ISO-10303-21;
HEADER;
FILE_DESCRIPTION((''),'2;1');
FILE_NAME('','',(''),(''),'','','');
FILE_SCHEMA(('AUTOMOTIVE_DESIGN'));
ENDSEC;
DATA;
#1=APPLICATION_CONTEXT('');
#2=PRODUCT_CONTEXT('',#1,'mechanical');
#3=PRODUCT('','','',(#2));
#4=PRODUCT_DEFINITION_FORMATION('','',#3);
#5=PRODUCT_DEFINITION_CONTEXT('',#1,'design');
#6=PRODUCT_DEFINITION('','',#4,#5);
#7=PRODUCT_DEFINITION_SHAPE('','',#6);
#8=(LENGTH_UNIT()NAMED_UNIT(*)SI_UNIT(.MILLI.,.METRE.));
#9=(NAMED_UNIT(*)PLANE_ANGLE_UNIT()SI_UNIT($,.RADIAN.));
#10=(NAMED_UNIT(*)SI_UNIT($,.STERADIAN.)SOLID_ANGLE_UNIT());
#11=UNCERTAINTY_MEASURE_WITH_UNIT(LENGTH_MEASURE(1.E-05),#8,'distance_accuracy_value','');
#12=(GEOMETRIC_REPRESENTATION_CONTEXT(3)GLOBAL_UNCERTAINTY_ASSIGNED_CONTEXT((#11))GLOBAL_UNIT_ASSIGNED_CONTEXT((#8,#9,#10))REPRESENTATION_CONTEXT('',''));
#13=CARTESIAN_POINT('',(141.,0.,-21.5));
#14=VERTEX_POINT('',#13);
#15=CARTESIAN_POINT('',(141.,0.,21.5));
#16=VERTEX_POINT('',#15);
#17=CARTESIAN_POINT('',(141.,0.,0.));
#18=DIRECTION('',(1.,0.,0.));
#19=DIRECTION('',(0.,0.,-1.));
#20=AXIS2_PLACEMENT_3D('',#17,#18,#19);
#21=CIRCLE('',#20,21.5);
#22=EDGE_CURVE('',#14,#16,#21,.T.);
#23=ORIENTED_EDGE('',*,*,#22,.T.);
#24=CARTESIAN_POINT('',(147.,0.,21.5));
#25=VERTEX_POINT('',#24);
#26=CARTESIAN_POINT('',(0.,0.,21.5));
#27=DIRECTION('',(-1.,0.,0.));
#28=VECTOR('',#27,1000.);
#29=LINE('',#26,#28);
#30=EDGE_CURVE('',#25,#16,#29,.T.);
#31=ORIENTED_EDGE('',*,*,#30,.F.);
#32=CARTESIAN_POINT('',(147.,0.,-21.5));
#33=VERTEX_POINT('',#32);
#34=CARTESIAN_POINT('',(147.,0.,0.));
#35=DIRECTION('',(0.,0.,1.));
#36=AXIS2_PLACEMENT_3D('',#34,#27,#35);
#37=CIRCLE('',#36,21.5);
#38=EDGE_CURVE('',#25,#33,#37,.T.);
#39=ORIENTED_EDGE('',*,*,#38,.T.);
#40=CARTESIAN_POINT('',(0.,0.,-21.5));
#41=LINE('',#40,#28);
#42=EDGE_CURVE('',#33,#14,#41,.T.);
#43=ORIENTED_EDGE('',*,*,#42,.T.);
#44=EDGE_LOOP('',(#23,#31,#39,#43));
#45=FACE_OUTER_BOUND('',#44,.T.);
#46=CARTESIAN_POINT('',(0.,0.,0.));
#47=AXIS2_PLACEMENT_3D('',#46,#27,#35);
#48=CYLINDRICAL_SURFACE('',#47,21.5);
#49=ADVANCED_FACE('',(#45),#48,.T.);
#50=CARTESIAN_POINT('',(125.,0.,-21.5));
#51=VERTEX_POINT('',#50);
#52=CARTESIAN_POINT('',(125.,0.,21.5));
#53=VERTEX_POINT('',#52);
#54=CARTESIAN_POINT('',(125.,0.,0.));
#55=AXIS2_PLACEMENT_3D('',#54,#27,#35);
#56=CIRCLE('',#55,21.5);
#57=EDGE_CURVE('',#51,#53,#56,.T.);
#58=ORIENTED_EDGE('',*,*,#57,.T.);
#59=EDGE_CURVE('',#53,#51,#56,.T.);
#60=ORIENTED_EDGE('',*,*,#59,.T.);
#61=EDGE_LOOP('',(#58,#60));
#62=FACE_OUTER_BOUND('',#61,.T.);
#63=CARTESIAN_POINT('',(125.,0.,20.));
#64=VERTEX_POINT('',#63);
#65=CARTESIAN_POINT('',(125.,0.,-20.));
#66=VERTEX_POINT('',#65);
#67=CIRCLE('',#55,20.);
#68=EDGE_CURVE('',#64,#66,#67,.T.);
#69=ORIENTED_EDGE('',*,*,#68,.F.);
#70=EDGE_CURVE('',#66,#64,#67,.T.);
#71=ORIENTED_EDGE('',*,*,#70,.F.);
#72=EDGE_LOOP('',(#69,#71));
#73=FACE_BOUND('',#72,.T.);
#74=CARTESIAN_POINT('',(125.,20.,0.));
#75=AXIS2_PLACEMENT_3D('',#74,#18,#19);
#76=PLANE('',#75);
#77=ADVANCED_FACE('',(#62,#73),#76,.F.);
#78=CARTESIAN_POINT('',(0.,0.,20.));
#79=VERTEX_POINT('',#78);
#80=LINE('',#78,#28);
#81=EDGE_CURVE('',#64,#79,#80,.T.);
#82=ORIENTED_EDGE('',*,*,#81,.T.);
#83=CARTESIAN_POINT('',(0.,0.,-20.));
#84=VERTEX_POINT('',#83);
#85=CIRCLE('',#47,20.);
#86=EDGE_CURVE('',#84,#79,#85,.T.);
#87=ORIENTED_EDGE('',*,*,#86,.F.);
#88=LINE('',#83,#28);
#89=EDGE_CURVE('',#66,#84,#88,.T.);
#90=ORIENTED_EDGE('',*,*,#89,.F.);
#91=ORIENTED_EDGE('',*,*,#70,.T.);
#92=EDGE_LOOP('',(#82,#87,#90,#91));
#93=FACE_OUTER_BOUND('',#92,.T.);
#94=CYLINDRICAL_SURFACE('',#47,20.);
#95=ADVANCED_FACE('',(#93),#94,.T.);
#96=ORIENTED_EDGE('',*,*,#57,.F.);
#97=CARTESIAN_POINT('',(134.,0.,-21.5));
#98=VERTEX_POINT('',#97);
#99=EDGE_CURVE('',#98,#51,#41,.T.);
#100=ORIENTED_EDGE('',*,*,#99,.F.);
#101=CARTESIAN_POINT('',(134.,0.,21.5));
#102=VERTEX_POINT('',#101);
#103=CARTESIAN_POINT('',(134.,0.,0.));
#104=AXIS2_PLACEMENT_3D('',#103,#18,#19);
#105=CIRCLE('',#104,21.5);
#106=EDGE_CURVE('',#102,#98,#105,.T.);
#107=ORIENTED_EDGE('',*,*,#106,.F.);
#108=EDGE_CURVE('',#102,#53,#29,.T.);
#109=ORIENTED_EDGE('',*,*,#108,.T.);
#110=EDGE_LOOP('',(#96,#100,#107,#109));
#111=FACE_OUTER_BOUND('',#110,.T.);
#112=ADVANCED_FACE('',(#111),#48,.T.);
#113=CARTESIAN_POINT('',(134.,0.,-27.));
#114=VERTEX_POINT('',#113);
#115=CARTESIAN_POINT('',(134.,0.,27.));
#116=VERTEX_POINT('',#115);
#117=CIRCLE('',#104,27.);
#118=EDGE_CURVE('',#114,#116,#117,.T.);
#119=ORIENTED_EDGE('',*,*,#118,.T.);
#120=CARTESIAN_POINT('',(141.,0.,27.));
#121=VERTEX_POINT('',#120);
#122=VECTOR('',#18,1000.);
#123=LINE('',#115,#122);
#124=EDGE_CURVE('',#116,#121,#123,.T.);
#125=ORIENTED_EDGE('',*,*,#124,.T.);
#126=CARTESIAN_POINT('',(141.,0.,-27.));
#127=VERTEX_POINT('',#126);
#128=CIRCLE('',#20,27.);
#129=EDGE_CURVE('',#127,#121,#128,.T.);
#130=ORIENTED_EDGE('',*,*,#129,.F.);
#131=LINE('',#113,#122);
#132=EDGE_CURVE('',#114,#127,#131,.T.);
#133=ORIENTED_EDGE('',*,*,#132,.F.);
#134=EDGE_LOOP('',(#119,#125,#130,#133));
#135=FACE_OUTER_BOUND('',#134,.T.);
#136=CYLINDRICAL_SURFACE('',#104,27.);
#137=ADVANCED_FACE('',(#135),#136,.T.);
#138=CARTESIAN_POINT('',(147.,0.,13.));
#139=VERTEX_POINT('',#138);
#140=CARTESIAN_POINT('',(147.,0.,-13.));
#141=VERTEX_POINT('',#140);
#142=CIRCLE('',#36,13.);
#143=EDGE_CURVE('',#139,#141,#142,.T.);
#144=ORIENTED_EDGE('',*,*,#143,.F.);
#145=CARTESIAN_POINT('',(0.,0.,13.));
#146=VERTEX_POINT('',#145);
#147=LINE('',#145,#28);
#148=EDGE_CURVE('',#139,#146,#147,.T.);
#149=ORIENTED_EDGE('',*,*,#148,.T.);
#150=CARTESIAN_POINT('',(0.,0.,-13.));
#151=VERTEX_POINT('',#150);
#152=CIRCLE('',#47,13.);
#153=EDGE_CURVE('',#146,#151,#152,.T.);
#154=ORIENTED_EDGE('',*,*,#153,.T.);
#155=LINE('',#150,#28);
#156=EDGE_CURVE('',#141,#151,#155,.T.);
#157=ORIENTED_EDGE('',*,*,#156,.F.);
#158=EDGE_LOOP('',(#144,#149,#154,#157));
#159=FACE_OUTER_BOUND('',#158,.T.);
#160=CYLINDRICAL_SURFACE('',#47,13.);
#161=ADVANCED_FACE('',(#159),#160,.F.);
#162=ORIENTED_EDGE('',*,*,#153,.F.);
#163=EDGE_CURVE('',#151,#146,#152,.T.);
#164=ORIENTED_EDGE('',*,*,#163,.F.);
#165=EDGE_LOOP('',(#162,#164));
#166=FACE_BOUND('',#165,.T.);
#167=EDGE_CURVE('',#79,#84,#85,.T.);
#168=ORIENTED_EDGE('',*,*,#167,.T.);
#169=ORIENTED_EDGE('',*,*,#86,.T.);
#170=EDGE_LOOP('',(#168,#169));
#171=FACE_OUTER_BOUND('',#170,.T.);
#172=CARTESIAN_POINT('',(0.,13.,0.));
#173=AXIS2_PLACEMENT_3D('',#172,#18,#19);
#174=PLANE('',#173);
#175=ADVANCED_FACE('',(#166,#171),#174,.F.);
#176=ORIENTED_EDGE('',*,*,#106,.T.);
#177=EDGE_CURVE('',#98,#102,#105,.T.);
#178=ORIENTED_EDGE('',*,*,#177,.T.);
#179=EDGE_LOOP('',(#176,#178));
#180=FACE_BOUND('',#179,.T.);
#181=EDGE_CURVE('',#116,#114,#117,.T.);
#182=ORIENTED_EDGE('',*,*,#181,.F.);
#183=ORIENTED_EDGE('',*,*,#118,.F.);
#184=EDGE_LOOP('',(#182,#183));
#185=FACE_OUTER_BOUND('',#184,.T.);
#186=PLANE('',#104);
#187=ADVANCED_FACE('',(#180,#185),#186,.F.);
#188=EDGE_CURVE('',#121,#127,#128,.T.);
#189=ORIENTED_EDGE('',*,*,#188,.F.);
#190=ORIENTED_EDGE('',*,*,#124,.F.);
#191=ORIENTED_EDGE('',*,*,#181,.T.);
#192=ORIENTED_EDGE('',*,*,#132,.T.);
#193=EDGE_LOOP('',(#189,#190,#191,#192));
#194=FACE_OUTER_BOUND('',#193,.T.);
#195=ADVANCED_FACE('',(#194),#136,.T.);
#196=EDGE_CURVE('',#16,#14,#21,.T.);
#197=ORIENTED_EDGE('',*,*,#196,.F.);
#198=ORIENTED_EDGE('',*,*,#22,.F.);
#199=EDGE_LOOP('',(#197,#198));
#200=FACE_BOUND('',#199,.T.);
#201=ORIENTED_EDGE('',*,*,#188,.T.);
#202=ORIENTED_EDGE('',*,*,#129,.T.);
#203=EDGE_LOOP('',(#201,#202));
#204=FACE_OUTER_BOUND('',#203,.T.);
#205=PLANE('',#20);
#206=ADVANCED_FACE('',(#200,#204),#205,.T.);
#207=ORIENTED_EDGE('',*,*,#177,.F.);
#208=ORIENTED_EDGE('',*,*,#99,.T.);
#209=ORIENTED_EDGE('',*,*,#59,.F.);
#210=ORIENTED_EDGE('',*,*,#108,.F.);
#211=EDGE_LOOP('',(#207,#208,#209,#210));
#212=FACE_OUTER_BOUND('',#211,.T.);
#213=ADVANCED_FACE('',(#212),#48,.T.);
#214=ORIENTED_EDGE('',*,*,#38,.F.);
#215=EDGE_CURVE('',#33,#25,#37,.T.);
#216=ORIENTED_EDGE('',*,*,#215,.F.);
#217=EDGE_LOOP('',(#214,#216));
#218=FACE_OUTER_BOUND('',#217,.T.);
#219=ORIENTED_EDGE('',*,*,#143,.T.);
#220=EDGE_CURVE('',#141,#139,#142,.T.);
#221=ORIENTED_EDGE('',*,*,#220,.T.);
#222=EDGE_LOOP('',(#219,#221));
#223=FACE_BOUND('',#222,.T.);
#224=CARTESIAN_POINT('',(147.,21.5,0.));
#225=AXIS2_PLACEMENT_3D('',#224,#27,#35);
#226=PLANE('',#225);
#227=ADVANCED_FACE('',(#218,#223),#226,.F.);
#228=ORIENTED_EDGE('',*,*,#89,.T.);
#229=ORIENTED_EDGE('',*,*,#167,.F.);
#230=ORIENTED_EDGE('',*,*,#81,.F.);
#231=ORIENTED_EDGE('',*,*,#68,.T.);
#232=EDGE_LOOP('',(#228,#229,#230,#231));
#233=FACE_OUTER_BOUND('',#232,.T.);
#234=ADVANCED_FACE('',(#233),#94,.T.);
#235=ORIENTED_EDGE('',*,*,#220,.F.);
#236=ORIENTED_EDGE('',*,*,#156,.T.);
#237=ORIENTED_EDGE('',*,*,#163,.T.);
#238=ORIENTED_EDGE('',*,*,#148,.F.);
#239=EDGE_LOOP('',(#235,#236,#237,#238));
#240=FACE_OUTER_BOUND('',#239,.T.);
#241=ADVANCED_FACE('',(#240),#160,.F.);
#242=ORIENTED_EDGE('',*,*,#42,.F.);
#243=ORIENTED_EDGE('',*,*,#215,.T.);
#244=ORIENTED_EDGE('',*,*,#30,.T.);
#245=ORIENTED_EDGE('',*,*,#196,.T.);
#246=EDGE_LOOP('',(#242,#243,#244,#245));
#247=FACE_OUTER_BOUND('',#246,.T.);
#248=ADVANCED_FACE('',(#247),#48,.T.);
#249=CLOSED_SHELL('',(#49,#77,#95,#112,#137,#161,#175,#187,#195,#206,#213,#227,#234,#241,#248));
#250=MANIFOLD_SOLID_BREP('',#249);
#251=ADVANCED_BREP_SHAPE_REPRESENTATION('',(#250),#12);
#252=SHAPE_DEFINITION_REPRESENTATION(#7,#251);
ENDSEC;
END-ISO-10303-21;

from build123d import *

# Parameters (mm, degrees)
EXTRUDE_START   = -6
SKETCH_2_R      = 27
SKETCH_2_R_2    = 21.5
EXTRUDE_1_DEPTH = 7


with BuildPart() as part:
    # 草图1 → 旋转1 (revolve)
    with BuildSketch(Plane.XY, mode=Mode.PRIVATE) as revolve_1_sk:
        Polygon((0, 13), (0, 20), (125, 20), (125, 21.5), (147, 21.5), (147, 13), align=None)
    revolve(revolve_1_sk.sketch.rotate(Axis((0, 0, 0), (1, 0, 0)), 90), axis=Axis((0, 0, 0), (1, 0, 0)))

    # 草图2 → 凸台-拉伸1 (add)
    with BuildSketch(Plane(origin=(147, 0, 0), x_dir=(0, 0, -1), z_dir=(1, 0, 0)).offset(EXTRUDE_START)):
        Circle(SKETCH_2_R)
        with Locations(Location((0, 0, 0), (0, 0, 180))):
            Circle(SKETCH_2_R_2, mode=Mode.SUBTRACT)
    extrude(amount=-EXTRUDE_1_DEPTH)


solid = part.part
